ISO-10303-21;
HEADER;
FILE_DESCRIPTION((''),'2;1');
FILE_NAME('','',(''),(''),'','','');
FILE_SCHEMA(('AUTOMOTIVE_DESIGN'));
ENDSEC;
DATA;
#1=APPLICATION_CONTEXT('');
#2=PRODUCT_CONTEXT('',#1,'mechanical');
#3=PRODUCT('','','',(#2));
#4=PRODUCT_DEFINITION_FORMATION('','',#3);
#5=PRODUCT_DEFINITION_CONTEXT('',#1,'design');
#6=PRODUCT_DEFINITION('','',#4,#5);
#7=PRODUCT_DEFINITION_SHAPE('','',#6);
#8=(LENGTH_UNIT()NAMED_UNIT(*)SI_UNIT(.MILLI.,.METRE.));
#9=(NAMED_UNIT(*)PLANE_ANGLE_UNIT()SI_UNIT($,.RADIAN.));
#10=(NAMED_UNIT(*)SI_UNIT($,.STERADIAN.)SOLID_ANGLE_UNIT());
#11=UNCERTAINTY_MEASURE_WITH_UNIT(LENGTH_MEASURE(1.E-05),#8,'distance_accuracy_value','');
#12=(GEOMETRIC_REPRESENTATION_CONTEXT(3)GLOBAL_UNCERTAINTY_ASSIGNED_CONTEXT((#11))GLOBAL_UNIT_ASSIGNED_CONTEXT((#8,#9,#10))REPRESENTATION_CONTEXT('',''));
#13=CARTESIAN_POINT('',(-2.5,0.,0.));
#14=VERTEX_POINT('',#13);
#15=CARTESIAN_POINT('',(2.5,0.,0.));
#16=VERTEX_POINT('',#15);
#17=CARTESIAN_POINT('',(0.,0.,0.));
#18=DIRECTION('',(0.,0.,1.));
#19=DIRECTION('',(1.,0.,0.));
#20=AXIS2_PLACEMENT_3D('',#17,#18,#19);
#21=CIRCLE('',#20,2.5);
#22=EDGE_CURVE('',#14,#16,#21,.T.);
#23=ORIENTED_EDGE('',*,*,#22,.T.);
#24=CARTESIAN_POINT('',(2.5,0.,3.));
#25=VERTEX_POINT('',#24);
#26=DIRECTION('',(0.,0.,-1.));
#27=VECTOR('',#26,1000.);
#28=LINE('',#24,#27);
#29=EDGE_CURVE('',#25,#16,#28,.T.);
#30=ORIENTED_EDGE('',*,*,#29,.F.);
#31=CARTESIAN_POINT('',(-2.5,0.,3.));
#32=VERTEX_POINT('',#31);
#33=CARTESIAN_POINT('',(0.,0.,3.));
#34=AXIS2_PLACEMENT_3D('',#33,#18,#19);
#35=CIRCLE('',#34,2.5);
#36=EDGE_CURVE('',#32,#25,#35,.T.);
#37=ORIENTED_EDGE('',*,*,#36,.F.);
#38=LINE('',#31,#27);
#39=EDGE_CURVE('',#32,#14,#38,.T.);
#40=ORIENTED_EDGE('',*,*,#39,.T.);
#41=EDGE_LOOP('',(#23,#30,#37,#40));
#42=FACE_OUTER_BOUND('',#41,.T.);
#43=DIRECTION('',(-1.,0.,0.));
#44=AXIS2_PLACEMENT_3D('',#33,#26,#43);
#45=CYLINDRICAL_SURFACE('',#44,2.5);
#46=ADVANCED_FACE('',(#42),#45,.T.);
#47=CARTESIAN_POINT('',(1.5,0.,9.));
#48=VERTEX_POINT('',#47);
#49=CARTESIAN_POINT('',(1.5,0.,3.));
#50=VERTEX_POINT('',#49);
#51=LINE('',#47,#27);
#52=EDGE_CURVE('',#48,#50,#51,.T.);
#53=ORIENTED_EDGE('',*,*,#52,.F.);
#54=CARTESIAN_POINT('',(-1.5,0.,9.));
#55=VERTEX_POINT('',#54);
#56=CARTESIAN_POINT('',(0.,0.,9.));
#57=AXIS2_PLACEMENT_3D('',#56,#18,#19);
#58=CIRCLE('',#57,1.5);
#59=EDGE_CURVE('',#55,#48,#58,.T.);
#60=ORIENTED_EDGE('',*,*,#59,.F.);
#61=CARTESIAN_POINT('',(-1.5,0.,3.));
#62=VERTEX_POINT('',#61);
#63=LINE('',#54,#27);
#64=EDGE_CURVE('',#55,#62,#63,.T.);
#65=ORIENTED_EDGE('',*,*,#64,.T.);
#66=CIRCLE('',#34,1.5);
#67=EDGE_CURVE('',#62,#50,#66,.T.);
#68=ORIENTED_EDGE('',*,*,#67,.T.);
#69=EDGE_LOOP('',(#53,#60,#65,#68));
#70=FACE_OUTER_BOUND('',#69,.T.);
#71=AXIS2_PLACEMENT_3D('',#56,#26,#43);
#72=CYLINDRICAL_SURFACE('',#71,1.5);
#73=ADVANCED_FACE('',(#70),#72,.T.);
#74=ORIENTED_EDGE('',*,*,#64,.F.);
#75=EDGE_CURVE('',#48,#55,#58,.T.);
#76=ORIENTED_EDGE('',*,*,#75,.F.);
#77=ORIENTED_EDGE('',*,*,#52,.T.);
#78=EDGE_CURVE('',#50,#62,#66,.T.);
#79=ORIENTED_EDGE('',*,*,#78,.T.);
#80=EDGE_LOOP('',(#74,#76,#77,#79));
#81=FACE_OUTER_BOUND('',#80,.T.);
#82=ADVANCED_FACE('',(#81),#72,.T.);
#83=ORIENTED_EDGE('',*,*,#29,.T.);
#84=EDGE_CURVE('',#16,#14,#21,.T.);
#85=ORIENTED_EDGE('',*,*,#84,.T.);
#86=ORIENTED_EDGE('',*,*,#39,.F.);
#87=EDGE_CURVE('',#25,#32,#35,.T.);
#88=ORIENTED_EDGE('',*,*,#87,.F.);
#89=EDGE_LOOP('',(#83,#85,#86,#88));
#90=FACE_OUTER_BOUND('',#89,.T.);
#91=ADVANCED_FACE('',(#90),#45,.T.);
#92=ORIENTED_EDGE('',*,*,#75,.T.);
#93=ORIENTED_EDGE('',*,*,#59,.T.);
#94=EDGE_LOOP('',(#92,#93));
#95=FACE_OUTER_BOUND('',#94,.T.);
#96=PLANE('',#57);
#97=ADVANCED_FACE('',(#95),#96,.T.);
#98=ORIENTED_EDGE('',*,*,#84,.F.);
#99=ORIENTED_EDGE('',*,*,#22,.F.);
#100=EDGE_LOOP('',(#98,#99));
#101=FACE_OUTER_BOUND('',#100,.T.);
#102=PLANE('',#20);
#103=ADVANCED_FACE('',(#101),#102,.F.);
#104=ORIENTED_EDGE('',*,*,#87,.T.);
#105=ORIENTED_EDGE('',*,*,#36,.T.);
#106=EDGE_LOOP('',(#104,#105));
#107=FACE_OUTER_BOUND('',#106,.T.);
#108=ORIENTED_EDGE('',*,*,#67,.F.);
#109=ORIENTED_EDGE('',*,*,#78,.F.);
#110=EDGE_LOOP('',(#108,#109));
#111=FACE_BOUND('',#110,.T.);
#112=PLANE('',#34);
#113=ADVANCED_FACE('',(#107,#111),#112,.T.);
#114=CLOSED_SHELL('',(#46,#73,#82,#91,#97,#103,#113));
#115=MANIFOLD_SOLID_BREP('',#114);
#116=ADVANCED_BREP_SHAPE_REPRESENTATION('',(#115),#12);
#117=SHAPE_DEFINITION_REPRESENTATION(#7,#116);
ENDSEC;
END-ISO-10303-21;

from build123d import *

# Parameters (mm, degrees)
SKETCH1_R           = 2.5
BOSS_EXTRUDE1_DEPTH = 3
SKETCH2_R           = 1.5
BOSS_EXTRUDE2_DEPTH = 6


with BuildPart() as part:
    # Sketch1 → Boss-Extrude1 (new body)
    with BuildSketch(Plane.XY):
        Circle(SKETCH1_R)
    extrude(amount=BOSS_EXTRUDE1_DEPTH)

    # Sketch2 → Boss-Extrude2 (add)
    with BuildSketch(Plane.XY.offset(3)):
        Circle(SKETCH2_R)
    extrude(amount=BOSS_EXTRUDE2_DEPTH)


solid = part.part
